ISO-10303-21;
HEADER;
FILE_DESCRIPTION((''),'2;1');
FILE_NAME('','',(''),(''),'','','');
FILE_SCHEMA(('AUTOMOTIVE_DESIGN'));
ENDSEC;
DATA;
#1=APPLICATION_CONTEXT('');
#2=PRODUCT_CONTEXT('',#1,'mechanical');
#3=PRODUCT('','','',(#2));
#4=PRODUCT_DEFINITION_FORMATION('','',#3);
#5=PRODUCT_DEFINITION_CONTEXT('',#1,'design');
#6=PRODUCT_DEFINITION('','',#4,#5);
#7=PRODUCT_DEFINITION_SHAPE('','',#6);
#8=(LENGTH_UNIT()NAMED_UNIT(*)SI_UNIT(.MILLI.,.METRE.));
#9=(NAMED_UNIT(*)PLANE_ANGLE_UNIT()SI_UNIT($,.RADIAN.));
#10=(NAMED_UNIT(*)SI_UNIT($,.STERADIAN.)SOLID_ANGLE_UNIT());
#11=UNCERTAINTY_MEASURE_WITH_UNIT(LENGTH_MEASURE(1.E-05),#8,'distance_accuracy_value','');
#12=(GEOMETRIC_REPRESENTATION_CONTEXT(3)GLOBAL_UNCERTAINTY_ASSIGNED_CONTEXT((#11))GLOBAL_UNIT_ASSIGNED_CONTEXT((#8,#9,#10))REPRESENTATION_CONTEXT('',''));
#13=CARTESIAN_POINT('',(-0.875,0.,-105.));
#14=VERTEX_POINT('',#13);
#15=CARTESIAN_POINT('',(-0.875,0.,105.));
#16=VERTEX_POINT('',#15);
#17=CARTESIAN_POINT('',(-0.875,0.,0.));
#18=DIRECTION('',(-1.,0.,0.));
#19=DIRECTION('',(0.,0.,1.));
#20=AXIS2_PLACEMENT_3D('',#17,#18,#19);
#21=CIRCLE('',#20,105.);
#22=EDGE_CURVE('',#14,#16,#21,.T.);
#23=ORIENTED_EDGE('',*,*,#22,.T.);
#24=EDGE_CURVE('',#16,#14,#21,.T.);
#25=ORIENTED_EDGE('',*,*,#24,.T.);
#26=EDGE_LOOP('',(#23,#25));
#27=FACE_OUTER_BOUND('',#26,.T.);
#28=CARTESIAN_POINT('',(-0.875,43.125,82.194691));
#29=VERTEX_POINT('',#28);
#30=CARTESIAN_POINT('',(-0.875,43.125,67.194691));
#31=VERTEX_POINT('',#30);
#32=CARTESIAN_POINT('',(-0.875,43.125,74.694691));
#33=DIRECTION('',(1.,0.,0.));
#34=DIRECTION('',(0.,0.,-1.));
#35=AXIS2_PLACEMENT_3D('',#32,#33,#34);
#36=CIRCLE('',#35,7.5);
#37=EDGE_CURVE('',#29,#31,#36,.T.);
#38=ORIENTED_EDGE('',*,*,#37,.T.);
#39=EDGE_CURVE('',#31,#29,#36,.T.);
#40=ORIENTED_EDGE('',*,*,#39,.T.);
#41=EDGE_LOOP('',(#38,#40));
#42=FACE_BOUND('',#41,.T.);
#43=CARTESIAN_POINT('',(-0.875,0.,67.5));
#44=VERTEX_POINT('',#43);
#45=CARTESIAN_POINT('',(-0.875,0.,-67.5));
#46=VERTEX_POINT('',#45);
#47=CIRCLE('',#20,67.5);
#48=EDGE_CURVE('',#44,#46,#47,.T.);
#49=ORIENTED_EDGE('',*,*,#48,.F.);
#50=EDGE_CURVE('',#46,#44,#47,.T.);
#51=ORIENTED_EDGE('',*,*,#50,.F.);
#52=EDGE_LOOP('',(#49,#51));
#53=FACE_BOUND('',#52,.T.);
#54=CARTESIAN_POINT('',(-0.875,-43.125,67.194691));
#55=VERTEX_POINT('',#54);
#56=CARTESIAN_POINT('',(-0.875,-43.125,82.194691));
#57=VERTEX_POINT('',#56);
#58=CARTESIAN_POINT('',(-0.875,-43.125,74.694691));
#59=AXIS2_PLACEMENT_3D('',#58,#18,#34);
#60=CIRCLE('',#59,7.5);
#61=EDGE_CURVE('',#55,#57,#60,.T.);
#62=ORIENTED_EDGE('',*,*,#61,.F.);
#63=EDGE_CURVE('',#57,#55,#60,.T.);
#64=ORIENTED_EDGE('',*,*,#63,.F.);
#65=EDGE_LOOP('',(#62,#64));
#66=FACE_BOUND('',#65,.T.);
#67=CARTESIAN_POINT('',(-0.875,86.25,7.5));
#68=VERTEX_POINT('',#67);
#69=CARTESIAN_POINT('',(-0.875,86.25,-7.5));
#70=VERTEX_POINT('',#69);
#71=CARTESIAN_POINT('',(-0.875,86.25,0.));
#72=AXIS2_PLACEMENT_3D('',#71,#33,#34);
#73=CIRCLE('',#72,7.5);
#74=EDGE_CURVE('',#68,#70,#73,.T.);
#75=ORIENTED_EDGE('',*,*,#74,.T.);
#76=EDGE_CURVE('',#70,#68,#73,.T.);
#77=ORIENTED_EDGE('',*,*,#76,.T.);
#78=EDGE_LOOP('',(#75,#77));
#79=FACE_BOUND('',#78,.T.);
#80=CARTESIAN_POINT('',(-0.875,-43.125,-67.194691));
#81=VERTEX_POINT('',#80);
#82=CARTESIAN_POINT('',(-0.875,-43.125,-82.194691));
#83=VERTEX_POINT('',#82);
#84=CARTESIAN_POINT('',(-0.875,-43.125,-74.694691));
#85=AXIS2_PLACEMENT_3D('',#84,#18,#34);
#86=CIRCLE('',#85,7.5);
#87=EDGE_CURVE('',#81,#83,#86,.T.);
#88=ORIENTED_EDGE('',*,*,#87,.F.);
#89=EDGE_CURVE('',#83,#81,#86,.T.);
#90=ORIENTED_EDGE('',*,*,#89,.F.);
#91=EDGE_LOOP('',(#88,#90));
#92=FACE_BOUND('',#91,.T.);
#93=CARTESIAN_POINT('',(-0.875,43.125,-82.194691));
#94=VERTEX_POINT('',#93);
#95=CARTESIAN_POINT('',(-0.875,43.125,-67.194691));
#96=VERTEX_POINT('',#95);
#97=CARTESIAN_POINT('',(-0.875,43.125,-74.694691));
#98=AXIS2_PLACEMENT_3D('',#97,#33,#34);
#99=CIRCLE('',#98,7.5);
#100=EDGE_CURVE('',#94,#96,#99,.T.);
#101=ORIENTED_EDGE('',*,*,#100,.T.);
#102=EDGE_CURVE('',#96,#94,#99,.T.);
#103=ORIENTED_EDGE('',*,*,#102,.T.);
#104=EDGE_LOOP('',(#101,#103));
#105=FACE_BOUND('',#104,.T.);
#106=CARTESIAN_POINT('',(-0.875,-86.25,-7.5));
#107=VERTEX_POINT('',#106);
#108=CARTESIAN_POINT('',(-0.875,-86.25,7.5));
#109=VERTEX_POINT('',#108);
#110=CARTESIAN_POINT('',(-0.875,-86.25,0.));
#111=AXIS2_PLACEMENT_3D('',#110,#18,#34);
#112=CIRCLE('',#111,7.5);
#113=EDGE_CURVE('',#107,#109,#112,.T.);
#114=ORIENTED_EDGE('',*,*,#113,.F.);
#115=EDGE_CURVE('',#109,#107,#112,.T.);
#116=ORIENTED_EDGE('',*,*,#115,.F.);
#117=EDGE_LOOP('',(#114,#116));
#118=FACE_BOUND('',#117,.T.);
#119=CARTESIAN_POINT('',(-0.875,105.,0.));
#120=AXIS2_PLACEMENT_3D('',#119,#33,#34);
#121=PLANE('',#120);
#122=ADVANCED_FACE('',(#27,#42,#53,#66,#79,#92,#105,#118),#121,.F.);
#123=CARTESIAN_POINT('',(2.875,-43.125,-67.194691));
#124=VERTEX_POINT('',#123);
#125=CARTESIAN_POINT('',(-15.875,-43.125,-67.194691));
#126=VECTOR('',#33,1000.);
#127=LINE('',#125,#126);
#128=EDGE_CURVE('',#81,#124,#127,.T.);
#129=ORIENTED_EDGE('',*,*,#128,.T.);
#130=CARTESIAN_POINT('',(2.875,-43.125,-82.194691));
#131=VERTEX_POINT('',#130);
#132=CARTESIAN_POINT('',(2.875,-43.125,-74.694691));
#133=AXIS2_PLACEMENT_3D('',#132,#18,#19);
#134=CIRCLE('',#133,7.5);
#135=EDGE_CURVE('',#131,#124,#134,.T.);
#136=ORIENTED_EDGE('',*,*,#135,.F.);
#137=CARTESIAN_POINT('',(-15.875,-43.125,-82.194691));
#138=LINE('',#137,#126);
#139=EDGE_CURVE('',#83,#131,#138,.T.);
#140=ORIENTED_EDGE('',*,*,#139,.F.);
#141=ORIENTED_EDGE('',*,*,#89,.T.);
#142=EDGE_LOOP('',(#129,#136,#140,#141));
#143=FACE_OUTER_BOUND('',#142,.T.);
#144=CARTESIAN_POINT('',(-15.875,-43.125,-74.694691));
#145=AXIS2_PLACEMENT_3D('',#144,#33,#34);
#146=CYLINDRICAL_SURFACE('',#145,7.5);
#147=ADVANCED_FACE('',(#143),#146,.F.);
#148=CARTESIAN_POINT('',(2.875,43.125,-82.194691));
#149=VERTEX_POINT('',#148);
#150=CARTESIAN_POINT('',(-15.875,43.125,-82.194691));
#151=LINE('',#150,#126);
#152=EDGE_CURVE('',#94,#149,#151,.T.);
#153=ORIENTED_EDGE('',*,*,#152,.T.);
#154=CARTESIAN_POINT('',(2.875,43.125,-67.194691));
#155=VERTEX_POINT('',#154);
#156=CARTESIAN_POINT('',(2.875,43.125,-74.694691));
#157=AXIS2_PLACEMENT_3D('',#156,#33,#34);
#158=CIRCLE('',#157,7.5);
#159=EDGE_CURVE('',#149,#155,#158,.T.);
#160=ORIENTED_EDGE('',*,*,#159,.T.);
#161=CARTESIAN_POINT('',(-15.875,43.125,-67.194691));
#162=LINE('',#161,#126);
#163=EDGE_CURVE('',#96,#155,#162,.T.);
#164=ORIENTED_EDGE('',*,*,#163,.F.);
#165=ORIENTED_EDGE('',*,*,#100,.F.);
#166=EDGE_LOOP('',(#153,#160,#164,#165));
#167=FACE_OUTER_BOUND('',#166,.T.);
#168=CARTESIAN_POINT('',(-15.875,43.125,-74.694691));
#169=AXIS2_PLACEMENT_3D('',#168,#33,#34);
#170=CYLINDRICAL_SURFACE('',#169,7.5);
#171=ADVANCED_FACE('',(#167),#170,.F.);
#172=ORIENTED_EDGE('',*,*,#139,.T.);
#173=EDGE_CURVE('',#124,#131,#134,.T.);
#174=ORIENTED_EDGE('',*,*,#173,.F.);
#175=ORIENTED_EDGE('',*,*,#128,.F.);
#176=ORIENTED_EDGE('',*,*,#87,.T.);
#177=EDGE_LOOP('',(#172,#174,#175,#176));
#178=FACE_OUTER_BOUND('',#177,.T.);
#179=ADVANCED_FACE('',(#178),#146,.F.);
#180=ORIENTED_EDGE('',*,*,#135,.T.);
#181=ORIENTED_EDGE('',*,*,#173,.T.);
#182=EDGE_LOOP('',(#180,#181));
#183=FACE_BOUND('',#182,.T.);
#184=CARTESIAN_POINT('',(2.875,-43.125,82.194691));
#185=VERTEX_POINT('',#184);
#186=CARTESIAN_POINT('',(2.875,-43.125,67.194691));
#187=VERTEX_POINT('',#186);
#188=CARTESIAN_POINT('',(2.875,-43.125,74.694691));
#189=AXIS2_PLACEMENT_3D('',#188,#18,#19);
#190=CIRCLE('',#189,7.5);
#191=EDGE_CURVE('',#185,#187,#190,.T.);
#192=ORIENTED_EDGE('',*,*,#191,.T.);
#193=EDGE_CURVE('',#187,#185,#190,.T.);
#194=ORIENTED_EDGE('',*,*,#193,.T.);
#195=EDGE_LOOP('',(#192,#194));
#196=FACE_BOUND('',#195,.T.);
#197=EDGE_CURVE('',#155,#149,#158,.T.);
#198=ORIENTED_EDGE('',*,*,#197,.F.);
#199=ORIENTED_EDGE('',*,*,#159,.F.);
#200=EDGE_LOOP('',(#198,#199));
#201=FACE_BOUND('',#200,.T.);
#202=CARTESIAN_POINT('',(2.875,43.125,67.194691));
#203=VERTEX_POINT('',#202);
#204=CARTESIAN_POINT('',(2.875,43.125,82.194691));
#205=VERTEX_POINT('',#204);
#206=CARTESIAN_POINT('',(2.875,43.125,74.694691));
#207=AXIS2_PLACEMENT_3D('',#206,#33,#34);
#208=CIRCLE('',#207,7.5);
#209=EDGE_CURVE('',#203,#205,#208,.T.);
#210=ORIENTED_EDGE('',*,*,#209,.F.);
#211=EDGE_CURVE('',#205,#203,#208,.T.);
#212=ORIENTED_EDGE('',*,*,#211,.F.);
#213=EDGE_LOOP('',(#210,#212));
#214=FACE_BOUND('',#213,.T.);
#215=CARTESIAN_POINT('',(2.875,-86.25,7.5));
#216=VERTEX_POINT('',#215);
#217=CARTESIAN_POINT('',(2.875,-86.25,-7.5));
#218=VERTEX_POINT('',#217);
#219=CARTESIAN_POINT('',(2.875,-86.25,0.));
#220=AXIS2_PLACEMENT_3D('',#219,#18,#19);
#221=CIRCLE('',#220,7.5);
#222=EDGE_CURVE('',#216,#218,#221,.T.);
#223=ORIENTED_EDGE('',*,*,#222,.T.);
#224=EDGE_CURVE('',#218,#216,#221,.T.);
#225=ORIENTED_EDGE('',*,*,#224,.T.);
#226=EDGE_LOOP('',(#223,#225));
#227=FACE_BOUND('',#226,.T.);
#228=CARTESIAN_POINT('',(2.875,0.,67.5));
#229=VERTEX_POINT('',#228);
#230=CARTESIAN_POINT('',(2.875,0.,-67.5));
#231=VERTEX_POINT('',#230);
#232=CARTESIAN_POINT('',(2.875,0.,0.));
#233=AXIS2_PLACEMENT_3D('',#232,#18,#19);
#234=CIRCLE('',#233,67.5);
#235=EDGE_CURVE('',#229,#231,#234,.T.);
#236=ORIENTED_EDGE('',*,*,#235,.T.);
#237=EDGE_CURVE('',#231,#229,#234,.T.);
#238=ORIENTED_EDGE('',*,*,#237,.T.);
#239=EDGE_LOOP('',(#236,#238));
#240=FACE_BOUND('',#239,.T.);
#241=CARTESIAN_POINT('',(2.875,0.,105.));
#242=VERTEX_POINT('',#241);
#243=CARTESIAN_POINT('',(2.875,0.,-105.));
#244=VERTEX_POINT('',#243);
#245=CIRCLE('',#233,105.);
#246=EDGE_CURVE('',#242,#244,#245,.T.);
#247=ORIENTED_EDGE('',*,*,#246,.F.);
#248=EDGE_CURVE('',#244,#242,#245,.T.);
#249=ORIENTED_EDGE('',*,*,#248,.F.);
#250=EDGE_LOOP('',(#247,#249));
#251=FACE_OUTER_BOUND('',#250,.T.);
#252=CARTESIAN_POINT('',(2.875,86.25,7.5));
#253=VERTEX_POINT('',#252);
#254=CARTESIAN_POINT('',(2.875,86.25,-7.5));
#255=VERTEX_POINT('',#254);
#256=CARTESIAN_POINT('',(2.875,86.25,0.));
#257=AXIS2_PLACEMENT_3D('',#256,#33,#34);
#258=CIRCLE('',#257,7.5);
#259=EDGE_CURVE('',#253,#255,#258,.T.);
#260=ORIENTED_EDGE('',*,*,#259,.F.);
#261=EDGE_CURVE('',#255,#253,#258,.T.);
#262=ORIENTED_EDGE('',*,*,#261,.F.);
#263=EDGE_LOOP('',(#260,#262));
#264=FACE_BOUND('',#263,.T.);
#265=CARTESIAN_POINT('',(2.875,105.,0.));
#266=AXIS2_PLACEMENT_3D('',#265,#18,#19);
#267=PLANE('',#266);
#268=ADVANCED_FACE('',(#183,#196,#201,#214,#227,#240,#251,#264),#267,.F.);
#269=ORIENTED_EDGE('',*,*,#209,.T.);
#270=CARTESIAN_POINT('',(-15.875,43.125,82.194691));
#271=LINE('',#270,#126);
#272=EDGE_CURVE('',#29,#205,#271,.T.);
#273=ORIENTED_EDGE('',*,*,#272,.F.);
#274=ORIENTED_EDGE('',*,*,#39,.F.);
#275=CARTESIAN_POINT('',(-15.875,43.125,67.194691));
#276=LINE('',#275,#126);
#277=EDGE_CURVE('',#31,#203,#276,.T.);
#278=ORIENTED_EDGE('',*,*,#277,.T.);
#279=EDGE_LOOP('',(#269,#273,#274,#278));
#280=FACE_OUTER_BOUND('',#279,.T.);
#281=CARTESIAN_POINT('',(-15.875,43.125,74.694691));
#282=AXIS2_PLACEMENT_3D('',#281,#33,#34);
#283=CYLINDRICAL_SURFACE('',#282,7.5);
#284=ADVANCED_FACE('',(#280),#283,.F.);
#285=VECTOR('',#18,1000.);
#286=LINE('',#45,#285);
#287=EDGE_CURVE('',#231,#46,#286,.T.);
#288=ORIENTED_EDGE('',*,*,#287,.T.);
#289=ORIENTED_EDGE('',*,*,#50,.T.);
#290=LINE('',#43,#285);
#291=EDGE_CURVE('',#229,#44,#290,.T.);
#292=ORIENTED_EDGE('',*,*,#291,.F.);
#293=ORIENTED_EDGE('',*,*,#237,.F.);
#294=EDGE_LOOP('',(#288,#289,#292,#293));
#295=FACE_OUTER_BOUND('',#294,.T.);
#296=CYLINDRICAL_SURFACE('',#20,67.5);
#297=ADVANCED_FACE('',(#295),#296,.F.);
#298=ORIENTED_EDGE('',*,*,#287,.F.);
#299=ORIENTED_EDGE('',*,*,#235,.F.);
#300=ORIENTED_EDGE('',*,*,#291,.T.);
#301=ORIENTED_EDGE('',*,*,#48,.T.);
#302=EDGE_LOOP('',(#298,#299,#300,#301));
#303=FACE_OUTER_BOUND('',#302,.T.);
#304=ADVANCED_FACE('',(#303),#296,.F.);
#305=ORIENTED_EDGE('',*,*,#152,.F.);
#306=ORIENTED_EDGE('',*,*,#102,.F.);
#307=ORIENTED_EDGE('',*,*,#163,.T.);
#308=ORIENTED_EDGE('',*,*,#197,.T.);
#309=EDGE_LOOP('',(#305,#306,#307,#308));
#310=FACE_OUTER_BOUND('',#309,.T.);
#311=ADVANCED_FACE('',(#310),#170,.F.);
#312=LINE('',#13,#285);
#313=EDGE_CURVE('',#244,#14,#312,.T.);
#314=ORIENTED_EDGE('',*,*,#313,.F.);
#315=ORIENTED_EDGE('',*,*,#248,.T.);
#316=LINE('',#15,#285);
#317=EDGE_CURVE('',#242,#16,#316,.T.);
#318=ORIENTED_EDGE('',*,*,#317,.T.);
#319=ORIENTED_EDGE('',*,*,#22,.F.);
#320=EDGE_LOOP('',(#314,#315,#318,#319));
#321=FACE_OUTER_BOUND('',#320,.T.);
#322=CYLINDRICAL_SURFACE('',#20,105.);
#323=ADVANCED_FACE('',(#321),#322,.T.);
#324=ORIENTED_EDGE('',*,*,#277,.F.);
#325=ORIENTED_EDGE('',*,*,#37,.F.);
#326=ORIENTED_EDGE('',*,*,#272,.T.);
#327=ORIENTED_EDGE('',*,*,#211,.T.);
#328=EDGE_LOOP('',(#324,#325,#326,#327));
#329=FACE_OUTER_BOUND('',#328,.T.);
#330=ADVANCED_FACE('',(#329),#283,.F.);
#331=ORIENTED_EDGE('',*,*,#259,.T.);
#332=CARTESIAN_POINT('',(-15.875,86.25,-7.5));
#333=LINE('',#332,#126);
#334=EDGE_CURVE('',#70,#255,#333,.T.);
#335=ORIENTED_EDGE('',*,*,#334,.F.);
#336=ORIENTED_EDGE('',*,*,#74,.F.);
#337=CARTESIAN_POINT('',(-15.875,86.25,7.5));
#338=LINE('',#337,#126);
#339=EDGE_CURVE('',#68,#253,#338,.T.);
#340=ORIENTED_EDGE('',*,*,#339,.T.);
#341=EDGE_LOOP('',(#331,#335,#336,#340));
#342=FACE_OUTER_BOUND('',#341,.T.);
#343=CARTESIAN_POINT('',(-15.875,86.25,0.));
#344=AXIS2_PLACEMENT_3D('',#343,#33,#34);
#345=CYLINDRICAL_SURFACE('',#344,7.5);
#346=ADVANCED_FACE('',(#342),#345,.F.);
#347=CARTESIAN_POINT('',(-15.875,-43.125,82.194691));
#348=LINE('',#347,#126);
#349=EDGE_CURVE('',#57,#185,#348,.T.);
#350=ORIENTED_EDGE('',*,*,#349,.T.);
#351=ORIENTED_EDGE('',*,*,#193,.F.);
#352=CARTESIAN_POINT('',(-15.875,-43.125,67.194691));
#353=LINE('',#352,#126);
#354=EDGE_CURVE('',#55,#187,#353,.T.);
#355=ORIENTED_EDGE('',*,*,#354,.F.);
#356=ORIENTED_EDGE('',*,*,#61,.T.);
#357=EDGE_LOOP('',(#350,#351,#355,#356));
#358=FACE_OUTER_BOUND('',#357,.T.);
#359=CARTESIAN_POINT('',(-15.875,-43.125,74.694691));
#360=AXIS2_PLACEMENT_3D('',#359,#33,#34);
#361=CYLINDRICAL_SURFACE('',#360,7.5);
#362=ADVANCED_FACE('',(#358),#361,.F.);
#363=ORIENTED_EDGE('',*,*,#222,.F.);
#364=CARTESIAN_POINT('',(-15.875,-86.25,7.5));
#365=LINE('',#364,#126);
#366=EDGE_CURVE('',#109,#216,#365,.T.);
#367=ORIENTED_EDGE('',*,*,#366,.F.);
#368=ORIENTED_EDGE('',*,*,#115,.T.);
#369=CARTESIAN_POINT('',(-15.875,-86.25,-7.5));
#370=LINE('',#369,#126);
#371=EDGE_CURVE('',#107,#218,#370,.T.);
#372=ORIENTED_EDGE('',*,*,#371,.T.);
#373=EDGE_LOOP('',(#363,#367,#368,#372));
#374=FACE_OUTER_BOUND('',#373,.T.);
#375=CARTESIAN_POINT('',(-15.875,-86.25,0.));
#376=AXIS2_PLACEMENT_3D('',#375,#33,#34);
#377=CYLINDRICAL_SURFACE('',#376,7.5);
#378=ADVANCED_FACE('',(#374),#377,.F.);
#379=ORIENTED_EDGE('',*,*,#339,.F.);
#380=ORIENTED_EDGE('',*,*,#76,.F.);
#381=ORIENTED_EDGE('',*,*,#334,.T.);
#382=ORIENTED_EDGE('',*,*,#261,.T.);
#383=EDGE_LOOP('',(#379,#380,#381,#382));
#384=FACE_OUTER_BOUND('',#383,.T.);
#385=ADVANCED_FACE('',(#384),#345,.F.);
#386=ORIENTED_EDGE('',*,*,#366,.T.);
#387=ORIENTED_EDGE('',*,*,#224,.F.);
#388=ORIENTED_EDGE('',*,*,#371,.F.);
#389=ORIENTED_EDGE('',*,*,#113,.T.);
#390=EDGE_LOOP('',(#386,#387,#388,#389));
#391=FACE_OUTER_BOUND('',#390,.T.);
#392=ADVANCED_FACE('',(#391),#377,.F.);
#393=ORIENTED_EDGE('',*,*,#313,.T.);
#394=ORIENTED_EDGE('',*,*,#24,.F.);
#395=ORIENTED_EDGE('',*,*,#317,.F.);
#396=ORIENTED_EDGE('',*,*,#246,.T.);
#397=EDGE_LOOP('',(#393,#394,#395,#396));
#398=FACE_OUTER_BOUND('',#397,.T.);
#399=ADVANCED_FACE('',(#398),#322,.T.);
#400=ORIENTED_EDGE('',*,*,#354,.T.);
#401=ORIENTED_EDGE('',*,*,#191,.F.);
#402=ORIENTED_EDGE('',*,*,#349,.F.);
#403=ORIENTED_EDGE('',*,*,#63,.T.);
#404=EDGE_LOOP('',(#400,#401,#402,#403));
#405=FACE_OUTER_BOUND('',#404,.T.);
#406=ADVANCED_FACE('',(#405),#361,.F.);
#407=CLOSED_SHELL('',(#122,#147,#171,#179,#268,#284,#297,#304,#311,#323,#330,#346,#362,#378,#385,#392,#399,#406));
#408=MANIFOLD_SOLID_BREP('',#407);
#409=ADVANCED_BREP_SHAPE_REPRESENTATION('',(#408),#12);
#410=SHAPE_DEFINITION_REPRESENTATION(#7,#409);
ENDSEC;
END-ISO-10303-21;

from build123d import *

# Parameters (mm, degrees)
SKETCH1_W          = 2
SKETCH1_H          = 20
SKETCH2_R          = 4
CUT_EXTRUDE1_DEPTH = 10
SCALE_1_SCALE      = 1.875


with BuildPart() as part:
    # Sketch1 → Revolve1 (revolve)
    with BuildSketch(Plane.XY, mode=Mode.PRIVATE) as revolve1_sk:
        with Locations((1, 46)):
            Rectangle(SKETCH1_W, SKETCH1_H)
    revolve(revolve1_sk.sketch.rotate(Axis((0, 0, 0), (1, 0, 0)), 90), axis=Axis((0, 0, 0), (1, 0, 0)))

    # Sketch2 → Cut-Extrude1 (cut)
    with BuildSketch(Plane(origin=(2, 0, 0), x_dir=(0, 0, -1), z_dir=(1, 0, 0))):
        with Locations((0, 46)):
            Circle(SKETCH2_R)
        with Locations((39.837168574, 23)):
            Circle(SKETCH2_R)
        with Locations((-39.837168574, 23)):
            Circle(SKETCH2_R)
        with Locations((-39.837168574, -23)):
            Circle(SKETCH2_R)
        with Locations((0, -46)):
            Circle(SKETCH2_R)
        with Locations((39.837168574, -23)):
            Circle(SKETCH2_R)
    extrude(amount=-CUT_EXTRUDE1_DEPTH, mode=Mode.SUBTRACT)


with BuildPart() as part_1:
    # Scale 1: scaled about (1, 0, 0)
    add(part.part.scale(SCALE_1_SCALE).moved(Location((-0.875, 0, 0))))


solid = part_1.part
